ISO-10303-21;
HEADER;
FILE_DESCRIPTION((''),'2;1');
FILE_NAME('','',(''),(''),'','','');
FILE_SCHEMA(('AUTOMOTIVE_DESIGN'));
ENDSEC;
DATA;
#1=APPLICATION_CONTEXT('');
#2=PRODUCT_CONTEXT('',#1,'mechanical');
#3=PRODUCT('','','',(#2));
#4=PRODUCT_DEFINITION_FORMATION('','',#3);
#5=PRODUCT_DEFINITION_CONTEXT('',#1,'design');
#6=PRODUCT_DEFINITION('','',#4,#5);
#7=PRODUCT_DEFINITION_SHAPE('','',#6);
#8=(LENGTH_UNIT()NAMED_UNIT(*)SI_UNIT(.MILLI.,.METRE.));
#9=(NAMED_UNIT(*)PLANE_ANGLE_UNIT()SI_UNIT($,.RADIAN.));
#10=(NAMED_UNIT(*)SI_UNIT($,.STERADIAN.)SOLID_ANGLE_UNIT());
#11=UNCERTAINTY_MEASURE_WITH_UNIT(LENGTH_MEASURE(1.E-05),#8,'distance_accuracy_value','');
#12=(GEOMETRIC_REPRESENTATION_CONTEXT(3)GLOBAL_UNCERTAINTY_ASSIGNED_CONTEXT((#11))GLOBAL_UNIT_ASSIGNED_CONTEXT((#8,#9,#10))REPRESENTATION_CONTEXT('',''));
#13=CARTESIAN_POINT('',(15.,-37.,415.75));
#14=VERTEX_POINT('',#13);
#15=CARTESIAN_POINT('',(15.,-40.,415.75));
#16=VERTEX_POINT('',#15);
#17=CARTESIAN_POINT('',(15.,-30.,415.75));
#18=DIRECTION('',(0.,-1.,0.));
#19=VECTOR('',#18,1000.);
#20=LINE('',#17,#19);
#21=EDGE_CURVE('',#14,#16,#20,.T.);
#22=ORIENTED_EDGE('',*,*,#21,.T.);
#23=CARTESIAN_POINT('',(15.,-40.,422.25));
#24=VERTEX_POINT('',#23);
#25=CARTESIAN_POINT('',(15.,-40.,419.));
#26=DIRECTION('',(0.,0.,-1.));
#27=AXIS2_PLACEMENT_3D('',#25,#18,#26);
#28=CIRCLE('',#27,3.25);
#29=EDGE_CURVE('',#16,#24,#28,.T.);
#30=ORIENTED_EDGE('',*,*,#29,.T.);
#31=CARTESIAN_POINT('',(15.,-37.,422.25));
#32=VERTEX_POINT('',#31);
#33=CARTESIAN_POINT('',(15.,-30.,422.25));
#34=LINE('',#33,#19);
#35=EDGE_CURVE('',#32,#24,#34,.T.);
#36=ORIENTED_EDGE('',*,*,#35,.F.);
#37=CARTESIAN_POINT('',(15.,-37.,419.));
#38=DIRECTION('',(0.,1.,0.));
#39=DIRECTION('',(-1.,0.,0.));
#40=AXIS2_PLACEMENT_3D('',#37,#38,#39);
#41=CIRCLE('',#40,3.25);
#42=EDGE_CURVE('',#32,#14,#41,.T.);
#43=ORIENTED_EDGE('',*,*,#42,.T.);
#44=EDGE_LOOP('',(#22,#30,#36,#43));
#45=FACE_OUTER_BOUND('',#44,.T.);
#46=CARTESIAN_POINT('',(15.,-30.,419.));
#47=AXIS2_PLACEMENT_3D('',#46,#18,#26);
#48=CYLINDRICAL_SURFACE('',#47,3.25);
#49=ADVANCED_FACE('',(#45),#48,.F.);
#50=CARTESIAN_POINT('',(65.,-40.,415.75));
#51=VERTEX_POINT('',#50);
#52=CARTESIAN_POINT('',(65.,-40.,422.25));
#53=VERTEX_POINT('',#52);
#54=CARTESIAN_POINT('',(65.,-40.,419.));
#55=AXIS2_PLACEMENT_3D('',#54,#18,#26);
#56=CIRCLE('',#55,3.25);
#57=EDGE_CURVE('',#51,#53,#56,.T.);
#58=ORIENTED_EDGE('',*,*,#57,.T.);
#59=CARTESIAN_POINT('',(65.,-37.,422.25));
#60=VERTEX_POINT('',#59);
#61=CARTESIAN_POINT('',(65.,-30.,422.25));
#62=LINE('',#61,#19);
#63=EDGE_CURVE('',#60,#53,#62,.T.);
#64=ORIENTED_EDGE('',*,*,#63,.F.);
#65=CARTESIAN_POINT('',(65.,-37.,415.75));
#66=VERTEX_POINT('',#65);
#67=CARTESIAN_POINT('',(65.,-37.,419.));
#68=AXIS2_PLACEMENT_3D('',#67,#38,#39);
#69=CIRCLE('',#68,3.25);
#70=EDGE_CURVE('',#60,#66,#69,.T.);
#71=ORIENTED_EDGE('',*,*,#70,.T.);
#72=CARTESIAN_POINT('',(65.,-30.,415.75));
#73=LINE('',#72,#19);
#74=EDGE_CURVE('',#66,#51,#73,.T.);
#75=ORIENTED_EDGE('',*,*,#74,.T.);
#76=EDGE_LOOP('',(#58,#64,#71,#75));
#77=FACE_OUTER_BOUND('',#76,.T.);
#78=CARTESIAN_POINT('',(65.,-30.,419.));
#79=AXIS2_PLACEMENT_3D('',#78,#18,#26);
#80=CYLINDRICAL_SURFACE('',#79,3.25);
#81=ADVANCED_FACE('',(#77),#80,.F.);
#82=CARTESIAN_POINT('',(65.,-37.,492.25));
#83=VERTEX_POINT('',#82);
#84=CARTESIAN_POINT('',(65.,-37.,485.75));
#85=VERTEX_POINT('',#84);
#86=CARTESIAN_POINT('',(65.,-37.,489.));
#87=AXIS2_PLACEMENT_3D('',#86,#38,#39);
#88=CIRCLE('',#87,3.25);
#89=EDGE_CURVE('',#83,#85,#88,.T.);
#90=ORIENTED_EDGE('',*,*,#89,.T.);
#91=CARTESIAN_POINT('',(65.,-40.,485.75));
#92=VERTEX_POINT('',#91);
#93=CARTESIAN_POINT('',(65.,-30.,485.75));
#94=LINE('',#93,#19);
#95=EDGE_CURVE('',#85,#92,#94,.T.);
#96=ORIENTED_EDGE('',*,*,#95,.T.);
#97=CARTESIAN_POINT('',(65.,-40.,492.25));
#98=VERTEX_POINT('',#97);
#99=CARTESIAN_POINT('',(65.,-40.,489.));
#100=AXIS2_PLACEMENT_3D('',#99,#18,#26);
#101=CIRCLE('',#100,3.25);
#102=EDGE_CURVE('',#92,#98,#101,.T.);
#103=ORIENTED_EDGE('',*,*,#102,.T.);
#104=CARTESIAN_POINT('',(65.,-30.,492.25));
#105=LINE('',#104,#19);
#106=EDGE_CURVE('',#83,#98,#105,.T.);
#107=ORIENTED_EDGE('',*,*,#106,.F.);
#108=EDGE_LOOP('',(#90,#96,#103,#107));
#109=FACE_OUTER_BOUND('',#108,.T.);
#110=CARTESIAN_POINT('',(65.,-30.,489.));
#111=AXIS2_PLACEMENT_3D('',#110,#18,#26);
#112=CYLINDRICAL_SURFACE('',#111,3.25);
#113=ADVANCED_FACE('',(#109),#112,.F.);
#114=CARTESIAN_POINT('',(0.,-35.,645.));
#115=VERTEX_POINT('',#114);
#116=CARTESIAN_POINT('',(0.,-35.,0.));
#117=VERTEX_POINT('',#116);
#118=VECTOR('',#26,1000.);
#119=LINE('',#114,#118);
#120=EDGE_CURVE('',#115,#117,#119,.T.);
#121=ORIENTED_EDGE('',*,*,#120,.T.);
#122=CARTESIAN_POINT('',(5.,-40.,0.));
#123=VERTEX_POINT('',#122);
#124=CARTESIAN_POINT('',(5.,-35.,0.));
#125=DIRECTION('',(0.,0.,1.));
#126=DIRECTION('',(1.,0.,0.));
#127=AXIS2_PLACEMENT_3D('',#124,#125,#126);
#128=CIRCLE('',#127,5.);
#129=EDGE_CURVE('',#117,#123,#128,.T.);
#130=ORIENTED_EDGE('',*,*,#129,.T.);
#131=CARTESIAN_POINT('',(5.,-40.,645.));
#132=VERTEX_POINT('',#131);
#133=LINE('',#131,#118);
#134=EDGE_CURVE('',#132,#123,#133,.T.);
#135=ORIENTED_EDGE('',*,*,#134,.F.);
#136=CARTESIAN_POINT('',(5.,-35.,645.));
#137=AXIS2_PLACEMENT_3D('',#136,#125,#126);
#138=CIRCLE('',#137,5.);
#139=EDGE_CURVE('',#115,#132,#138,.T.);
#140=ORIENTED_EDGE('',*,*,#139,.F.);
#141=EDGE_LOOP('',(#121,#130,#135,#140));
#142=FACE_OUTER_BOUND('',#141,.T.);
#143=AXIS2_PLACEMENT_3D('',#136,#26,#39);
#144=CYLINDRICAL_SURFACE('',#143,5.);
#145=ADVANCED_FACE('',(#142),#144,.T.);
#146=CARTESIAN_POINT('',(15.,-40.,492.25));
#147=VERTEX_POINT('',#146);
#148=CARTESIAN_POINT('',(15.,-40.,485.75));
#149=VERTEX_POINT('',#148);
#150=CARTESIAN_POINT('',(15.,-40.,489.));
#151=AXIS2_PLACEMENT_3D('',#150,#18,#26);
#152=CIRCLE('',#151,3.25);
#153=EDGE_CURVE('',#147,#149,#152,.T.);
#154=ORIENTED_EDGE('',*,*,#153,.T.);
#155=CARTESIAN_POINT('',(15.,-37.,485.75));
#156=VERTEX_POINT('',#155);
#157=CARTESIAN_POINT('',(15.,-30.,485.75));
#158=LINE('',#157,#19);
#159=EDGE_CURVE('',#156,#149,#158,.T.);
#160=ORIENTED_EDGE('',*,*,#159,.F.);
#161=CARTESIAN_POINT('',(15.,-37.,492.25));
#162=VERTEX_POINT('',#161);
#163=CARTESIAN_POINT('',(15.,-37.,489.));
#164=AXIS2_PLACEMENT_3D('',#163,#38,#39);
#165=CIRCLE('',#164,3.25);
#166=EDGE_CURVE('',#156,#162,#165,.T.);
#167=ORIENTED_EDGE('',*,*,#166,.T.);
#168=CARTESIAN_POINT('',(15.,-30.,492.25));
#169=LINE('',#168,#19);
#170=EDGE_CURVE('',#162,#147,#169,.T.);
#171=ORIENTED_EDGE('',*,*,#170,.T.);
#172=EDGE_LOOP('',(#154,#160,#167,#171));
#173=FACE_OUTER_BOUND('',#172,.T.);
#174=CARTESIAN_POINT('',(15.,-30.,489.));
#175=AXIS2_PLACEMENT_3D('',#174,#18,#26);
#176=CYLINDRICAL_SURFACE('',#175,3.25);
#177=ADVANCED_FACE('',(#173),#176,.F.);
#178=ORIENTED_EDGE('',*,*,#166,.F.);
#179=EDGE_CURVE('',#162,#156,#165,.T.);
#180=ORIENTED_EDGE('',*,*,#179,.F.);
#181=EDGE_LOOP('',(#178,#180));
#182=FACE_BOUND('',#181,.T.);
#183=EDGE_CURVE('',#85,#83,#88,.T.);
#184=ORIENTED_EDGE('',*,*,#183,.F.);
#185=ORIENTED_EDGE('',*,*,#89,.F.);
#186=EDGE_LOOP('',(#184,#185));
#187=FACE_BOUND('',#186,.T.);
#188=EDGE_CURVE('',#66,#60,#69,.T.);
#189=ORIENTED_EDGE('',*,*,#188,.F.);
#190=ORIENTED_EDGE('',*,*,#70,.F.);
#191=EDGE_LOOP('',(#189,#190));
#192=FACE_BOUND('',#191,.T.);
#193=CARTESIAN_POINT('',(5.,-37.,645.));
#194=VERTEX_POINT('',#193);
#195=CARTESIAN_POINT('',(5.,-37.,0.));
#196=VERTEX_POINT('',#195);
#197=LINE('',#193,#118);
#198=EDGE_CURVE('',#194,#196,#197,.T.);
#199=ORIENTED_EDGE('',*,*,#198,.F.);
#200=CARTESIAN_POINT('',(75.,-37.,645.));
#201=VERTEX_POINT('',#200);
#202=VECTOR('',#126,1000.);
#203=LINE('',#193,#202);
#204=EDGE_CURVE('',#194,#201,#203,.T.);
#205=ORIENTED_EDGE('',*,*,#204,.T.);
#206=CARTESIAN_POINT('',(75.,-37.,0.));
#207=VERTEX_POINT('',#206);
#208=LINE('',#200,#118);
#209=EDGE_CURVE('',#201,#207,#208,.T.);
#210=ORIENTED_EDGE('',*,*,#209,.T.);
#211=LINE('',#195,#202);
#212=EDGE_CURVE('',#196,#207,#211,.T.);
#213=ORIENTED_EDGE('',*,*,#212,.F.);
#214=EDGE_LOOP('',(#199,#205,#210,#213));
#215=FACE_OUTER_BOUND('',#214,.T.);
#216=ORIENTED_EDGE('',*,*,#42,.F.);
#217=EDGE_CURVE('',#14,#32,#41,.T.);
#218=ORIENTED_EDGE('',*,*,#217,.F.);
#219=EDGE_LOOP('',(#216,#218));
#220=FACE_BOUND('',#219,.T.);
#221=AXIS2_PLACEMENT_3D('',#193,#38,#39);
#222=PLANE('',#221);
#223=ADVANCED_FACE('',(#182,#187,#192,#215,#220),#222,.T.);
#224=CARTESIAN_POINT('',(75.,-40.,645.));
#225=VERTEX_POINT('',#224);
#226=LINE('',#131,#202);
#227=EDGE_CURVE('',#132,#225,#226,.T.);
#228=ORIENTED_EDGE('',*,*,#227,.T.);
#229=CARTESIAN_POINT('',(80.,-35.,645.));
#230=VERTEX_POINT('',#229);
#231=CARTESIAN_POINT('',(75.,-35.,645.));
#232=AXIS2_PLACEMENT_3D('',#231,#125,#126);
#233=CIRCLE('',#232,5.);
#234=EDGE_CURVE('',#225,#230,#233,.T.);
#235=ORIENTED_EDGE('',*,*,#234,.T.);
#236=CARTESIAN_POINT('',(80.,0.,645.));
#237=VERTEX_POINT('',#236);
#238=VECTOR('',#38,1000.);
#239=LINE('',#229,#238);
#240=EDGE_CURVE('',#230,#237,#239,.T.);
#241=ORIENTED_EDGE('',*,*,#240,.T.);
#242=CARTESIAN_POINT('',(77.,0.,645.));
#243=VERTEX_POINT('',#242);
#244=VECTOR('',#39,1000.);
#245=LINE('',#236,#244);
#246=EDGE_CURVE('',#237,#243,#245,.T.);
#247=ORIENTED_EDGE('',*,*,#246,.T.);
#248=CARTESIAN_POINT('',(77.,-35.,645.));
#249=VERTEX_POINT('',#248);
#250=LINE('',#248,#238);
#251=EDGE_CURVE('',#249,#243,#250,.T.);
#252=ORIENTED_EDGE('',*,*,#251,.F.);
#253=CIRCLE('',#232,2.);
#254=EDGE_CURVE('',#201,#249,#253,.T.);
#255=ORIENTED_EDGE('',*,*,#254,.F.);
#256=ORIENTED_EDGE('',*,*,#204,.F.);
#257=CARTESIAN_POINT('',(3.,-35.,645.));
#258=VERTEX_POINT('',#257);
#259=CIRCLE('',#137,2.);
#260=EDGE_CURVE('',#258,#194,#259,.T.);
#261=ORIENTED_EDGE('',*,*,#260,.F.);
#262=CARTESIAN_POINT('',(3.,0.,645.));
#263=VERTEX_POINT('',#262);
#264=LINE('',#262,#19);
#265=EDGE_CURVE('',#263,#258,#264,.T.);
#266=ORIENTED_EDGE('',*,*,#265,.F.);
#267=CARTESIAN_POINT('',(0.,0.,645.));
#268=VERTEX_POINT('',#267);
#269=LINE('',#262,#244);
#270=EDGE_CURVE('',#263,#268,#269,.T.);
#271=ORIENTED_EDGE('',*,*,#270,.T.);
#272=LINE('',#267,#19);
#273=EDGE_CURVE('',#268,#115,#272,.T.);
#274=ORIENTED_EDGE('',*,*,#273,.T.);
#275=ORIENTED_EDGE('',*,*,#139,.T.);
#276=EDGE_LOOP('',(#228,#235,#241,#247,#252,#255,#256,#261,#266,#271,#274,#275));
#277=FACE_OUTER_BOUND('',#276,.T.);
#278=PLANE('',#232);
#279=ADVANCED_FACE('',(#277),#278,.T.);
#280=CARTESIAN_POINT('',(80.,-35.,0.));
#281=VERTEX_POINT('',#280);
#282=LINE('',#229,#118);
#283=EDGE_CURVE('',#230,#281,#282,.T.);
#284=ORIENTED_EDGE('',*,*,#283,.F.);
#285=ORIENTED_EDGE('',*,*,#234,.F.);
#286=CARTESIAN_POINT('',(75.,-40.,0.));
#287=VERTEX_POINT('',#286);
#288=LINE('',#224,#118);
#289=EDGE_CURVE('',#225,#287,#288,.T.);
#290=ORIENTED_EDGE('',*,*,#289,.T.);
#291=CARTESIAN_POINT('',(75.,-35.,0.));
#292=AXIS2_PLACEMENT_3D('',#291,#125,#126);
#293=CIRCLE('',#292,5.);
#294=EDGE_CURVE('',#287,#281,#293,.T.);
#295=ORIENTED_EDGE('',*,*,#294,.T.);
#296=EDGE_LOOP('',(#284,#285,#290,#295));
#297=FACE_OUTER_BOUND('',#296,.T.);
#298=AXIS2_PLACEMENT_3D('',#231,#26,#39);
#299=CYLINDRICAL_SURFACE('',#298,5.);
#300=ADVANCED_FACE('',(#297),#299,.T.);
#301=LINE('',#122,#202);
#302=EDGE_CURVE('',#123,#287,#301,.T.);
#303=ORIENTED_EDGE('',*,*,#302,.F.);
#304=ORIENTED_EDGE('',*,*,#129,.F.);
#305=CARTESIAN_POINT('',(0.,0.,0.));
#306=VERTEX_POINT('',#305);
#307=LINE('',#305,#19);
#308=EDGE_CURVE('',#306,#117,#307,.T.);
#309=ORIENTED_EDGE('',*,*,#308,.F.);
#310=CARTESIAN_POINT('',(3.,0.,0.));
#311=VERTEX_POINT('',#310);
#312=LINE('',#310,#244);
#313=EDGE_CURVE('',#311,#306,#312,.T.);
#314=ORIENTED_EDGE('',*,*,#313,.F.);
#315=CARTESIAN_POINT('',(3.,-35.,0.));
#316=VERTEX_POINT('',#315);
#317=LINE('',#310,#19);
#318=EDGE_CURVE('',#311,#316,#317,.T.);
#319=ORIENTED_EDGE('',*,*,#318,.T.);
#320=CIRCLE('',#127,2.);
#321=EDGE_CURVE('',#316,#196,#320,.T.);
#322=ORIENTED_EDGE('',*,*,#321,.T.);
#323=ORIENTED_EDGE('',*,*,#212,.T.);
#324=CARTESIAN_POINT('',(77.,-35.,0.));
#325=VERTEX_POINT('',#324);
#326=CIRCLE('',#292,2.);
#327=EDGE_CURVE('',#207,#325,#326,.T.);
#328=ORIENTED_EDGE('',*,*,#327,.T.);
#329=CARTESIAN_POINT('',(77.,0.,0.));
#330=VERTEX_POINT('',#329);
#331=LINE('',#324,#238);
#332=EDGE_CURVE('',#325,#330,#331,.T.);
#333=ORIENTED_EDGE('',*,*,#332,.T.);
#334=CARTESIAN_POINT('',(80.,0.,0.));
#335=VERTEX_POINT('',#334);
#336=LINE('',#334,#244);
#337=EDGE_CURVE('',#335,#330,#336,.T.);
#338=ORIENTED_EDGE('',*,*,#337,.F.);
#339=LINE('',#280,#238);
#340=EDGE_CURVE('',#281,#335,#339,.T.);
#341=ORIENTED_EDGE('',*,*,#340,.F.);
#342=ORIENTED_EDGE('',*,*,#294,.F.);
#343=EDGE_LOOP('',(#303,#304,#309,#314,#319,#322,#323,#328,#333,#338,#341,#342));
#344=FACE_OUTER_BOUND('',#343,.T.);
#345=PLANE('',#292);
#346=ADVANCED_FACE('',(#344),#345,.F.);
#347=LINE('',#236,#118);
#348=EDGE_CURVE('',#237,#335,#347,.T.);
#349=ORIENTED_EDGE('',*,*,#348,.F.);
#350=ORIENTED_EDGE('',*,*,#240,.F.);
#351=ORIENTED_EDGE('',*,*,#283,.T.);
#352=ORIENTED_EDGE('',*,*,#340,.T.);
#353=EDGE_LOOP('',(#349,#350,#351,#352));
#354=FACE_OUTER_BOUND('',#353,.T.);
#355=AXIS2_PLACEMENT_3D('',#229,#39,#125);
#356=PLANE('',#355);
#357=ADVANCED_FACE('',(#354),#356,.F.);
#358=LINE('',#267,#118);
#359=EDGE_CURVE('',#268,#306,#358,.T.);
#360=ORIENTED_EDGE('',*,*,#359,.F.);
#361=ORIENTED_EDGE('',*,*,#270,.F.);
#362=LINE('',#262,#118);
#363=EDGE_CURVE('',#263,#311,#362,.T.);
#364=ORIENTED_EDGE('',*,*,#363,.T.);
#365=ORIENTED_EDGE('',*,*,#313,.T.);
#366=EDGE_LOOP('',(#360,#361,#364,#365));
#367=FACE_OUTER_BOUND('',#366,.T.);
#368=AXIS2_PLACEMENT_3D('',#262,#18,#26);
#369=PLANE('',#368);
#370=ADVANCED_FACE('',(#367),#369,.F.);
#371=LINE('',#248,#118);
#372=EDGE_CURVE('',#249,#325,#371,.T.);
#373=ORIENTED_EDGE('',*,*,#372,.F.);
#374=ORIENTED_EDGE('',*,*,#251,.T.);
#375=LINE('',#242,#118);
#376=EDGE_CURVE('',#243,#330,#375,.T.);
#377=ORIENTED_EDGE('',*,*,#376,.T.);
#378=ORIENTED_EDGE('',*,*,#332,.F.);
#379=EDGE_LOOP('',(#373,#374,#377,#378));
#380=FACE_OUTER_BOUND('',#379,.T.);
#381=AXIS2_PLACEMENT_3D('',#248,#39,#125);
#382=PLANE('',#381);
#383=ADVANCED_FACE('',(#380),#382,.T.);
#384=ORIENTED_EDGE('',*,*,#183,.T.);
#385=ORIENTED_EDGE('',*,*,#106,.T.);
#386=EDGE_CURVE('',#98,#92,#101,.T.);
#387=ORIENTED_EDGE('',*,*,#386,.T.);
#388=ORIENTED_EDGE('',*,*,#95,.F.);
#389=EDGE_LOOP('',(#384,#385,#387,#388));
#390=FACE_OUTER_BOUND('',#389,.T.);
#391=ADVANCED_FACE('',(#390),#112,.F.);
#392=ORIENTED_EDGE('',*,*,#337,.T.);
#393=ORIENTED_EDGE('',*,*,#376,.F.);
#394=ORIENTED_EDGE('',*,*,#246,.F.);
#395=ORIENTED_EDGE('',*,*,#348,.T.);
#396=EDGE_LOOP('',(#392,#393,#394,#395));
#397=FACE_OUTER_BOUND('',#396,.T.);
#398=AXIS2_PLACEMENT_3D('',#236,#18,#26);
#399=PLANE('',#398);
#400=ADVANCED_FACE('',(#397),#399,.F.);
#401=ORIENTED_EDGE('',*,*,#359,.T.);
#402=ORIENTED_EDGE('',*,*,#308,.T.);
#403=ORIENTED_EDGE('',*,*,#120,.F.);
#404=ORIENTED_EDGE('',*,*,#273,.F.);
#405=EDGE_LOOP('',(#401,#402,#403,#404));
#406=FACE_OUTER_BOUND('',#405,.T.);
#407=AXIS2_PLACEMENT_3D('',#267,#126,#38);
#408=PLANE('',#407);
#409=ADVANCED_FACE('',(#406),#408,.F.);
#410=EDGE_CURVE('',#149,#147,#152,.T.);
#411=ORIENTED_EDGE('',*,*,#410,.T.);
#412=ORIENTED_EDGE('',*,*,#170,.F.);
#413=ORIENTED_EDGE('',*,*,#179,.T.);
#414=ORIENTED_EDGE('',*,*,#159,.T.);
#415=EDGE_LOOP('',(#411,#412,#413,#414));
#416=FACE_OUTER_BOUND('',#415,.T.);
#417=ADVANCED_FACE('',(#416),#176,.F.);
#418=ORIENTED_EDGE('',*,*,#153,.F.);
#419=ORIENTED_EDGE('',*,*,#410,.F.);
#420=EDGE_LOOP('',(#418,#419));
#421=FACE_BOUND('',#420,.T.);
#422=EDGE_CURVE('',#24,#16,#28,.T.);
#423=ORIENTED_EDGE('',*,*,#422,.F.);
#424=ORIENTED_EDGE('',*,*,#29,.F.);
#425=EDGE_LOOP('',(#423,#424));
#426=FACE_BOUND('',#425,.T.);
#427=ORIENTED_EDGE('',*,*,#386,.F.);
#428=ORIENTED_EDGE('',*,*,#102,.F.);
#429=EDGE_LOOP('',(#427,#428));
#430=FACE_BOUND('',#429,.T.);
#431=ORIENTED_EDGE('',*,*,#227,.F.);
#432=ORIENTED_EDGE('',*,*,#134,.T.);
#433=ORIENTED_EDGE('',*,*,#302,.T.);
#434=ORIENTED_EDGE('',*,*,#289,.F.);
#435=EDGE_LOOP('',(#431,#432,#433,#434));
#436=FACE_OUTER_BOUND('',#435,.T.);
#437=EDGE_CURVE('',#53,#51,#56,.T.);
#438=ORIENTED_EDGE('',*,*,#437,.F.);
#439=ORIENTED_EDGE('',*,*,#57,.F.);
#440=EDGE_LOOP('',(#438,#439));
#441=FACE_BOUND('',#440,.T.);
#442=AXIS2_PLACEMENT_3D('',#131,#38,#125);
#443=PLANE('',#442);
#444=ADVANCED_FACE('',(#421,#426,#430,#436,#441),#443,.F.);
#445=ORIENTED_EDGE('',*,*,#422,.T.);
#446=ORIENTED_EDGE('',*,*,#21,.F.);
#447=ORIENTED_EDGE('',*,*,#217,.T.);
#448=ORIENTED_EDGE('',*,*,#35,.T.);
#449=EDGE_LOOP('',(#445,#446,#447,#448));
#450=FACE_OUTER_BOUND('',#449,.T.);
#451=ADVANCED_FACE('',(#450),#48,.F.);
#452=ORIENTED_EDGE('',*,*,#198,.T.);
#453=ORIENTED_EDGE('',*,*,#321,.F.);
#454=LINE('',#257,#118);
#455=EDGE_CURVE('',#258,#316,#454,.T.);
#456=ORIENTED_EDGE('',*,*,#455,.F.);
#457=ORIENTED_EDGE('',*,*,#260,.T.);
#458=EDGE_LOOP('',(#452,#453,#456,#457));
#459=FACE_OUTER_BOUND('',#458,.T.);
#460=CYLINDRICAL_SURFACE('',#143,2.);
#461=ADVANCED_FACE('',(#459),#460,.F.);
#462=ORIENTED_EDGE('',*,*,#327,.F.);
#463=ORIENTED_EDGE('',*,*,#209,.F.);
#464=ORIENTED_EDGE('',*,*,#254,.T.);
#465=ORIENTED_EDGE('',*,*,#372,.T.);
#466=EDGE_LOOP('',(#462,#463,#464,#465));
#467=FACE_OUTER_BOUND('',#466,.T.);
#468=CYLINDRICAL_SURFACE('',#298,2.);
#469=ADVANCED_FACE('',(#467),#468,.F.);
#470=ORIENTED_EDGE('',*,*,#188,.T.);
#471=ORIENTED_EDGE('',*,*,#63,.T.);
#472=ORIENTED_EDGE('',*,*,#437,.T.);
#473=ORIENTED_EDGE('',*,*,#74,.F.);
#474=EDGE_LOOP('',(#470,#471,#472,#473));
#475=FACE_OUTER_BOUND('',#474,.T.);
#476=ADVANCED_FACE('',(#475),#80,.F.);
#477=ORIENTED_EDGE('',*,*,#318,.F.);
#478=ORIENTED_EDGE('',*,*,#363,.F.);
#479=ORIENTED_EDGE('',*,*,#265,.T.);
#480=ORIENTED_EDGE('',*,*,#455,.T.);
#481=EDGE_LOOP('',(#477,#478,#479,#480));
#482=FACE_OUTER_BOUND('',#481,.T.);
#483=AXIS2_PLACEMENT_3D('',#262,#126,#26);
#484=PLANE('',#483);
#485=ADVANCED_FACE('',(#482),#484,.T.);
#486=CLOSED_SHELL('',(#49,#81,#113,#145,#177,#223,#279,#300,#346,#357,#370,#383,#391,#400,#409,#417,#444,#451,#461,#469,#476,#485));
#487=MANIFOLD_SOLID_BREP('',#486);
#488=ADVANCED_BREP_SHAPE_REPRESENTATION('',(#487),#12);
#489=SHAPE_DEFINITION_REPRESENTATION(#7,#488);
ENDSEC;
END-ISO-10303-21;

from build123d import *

# Parameters (mm, degrees)
BOSS_EXTRUDE1_DEPTH = 645
SKETCH2_R           = 3.25
CUT_EXTRUDE1_DEPTH  = 10


with BuildPart() as part:
    # Sketch1 → Boss-Extrude1 (new body)
    with BuildSketch(Plane.XY):
        with BuildLine():
            Line((0, 0), (0, -35))
            ThreePointArc((0, -35), (1.464466094, -38.535533906), (5, -40))
            Line((5, -40), (75, -40))
            ThreePointArc((75, -40), (78.535533906, -38.535533906), (80, -35))
            Line((80, -35), (80, 0))
            Line((80, 0), (77, 0))
            Line((77, 0), (77, -35))
            ThreePointArc((77, -35), (76.414213562, -36.414213562), (75, -37))
            Line((75, -37), (5, -37))
            ThreePointArc((5, -37), (3.585786438, -36.414213562), (3, -35))
            Line((3, -35), (3, 0))
            Line((3, 0), (0, 0))
        make_face()
    extrude(amount=BOSS_EXTRUDE1_DEPTH)

    # Sketch2 → Cut-Extrude1 (cut)
    with BuildSketch(Plane.XZ.offset(40)):
        with Locations(Location((15, 489, 0), (0, 0, 270))):
            Circle(SKETCH2_R)
        with Locations(Location((65, 489, 0), (0, 0, 270))):
            Circle(SKETCH2_R)
        with Locations(Location((15, 419, 0), (0, 0, 270))):
            Circle(SKETCH2_R)
        with Locations(Location((65, 419, 0), (0, 0, 270))):
            Circle(SKETCH2_R)
    extrude(amount=-CUT_EXTRUDE1_DEPTH, mode=Mode.SUBTRACT)


solid = part.part
